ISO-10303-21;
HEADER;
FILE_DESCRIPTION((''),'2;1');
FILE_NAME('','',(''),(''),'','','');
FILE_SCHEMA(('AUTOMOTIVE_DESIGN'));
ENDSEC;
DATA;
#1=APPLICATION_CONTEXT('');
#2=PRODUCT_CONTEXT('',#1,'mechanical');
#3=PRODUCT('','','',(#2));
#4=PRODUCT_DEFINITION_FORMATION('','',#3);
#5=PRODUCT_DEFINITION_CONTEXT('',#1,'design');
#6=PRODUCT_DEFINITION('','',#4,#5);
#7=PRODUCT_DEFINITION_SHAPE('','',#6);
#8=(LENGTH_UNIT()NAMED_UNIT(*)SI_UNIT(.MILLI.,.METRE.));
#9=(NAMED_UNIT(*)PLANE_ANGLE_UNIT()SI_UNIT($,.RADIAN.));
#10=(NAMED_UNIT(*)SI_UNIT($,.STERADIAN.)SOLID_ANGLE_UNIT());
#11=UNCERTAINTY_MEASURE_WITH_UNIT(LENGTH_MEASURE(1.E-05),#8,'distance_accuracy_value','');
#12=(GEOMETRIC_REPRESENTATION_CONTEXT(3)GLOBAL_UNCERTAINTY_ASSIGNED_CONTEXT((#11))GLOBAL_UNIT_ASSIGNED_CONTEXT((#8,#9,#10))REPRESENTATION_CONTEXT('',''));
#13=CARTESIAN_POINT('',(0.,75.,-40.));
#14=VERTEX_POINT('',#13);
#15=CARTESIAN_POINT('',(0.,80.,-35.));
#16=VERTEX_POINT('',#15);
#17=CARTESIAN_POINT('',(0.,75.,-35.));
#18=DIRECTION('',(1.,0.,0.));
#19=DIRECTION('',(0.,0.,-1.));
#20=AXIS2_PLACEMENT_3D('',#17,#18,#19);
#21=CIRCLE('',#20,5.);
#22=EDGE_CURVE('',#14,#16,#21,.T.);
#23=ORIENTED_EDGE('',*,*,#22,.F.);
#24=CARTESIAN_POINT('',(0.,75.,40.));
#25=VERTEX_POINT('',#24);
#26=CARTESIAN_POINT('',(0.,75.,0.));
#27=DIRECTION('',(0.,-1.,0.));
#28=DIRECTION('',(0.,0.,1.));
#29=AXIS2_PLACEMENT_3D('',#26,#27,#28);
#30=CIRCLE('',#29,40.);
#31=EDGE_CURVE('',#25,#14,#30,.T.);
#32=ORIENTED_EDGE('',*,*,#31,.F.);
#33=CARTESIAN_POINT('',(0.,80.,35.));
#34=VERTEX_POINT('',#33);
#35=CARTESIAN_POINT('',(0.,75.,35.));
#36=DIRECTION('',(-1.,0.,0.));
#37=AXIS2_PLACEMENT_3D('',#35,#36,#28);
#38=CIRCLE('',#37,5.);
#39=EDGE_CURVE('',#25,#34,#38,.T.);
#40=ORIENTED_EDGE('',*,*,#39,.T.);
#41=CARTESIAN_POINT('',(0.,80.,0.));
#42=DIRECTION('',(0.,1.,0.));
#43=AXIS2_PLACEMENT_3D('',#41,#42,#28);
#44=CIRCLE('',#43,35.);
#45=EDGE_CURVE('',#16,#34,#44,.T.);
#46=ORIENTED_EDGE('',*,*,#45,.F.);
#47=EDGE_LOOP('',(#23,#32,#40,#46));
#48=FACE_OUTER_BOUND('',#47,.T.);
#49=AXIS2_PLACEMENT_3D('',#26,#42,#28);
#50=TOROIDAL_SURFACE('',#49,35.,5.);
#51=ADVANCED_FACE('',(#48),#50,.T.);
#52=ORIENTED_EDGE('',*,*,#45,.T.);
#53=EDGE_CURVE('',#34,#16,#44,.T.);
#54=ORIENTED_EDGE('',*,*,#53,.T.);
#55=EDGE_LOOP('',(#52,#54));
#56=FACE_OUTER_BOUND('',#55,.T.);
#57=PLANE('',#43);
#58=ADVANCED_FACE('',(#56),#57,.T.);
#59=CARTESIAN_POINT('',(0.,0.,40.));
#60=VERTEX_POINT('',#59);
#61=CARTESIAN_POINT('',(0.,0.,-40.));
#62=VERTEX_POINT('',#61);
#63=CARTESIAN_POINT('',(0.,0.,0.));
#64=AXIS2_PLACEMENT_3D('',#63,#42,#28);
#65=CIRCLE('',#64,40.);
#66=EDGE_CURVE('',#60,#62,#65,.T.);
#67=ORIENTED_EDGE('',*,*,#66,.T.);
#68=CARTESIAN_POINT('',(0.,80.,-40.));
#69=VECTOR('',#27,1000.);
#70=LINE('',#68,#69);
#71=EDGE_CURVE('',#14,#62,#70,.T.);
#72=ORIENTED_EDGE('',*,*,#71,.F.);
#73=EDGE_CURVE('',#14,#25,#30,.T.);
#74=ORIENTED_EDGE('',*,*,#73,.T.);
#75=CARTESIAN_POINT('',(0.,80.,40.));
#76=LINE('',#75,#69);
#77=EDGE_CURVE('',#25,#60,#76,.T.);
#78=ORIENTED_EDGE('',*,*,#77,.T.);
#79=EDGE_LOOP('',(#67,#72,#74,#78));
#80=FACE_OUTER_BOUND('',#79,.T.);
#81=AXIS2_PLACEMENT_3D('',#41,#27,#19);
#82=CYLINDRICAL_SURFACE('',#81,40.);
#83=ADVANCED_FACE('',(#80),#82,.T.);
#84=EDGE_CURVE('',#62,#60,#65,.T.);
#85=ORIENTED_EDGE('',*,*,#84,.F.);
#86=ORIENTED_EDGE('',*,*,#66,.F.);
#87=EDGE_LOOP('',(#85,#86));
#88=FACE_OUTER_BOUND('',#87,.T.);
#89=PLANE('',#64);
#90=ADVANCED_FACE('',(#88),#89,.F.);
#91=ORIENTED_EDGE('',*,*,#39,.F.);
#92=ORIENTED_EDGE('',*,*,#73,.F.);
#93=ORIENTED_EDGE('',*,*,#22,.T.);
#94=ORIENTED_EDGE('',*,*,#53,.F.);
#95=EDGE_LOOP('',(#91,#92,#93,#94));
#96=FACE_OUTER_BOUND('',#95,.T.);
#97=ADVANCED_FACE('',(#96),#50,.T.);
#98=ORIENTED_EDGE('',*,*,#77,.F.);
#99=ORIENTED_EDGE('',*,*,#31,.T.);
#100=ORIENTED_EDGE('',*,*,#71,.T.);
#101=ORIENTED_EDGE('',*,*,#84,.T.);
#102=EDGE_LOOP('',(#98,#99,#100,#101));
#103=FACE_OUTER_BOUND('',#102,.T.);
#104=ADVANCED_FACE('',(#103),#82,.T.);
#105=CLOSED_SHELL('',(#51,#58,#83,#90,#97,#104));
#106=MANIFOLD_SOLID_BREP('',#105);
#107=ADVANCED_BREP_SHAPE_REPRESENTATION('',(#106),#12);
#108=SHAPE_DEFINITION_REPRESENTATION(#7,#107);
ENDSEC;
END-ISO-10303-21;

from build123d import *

# Parameters (mm, degrees)
SKETCH1_R           = 40
BOSS_EXTRUDE1_DEPTH = 80
FILLET1_R           = 5


with BuildPart() as part:
    # Sketch1 → Boss-Extrude1 (new body)
    with BuildSketch(Plane(origin=(0, 0, 0), x_dir=(1, 0, 0), z_dir=(0, 1, 0))):
        with Locations(Location((0, 0, 0), (0, 0, 270))):
            Circle(SKETCH1_R)
    extrude(amount=BOSS_EXTRUDE1_DEPTH)

    # Fillet1
    fillet1_edges = [part.edges().sort_by_distance(p)[0] for p in [
        (0, 80, -40),
    ]]
    fillet(fillet1_edges, radius=FILLET1_R)


solid = part.part
